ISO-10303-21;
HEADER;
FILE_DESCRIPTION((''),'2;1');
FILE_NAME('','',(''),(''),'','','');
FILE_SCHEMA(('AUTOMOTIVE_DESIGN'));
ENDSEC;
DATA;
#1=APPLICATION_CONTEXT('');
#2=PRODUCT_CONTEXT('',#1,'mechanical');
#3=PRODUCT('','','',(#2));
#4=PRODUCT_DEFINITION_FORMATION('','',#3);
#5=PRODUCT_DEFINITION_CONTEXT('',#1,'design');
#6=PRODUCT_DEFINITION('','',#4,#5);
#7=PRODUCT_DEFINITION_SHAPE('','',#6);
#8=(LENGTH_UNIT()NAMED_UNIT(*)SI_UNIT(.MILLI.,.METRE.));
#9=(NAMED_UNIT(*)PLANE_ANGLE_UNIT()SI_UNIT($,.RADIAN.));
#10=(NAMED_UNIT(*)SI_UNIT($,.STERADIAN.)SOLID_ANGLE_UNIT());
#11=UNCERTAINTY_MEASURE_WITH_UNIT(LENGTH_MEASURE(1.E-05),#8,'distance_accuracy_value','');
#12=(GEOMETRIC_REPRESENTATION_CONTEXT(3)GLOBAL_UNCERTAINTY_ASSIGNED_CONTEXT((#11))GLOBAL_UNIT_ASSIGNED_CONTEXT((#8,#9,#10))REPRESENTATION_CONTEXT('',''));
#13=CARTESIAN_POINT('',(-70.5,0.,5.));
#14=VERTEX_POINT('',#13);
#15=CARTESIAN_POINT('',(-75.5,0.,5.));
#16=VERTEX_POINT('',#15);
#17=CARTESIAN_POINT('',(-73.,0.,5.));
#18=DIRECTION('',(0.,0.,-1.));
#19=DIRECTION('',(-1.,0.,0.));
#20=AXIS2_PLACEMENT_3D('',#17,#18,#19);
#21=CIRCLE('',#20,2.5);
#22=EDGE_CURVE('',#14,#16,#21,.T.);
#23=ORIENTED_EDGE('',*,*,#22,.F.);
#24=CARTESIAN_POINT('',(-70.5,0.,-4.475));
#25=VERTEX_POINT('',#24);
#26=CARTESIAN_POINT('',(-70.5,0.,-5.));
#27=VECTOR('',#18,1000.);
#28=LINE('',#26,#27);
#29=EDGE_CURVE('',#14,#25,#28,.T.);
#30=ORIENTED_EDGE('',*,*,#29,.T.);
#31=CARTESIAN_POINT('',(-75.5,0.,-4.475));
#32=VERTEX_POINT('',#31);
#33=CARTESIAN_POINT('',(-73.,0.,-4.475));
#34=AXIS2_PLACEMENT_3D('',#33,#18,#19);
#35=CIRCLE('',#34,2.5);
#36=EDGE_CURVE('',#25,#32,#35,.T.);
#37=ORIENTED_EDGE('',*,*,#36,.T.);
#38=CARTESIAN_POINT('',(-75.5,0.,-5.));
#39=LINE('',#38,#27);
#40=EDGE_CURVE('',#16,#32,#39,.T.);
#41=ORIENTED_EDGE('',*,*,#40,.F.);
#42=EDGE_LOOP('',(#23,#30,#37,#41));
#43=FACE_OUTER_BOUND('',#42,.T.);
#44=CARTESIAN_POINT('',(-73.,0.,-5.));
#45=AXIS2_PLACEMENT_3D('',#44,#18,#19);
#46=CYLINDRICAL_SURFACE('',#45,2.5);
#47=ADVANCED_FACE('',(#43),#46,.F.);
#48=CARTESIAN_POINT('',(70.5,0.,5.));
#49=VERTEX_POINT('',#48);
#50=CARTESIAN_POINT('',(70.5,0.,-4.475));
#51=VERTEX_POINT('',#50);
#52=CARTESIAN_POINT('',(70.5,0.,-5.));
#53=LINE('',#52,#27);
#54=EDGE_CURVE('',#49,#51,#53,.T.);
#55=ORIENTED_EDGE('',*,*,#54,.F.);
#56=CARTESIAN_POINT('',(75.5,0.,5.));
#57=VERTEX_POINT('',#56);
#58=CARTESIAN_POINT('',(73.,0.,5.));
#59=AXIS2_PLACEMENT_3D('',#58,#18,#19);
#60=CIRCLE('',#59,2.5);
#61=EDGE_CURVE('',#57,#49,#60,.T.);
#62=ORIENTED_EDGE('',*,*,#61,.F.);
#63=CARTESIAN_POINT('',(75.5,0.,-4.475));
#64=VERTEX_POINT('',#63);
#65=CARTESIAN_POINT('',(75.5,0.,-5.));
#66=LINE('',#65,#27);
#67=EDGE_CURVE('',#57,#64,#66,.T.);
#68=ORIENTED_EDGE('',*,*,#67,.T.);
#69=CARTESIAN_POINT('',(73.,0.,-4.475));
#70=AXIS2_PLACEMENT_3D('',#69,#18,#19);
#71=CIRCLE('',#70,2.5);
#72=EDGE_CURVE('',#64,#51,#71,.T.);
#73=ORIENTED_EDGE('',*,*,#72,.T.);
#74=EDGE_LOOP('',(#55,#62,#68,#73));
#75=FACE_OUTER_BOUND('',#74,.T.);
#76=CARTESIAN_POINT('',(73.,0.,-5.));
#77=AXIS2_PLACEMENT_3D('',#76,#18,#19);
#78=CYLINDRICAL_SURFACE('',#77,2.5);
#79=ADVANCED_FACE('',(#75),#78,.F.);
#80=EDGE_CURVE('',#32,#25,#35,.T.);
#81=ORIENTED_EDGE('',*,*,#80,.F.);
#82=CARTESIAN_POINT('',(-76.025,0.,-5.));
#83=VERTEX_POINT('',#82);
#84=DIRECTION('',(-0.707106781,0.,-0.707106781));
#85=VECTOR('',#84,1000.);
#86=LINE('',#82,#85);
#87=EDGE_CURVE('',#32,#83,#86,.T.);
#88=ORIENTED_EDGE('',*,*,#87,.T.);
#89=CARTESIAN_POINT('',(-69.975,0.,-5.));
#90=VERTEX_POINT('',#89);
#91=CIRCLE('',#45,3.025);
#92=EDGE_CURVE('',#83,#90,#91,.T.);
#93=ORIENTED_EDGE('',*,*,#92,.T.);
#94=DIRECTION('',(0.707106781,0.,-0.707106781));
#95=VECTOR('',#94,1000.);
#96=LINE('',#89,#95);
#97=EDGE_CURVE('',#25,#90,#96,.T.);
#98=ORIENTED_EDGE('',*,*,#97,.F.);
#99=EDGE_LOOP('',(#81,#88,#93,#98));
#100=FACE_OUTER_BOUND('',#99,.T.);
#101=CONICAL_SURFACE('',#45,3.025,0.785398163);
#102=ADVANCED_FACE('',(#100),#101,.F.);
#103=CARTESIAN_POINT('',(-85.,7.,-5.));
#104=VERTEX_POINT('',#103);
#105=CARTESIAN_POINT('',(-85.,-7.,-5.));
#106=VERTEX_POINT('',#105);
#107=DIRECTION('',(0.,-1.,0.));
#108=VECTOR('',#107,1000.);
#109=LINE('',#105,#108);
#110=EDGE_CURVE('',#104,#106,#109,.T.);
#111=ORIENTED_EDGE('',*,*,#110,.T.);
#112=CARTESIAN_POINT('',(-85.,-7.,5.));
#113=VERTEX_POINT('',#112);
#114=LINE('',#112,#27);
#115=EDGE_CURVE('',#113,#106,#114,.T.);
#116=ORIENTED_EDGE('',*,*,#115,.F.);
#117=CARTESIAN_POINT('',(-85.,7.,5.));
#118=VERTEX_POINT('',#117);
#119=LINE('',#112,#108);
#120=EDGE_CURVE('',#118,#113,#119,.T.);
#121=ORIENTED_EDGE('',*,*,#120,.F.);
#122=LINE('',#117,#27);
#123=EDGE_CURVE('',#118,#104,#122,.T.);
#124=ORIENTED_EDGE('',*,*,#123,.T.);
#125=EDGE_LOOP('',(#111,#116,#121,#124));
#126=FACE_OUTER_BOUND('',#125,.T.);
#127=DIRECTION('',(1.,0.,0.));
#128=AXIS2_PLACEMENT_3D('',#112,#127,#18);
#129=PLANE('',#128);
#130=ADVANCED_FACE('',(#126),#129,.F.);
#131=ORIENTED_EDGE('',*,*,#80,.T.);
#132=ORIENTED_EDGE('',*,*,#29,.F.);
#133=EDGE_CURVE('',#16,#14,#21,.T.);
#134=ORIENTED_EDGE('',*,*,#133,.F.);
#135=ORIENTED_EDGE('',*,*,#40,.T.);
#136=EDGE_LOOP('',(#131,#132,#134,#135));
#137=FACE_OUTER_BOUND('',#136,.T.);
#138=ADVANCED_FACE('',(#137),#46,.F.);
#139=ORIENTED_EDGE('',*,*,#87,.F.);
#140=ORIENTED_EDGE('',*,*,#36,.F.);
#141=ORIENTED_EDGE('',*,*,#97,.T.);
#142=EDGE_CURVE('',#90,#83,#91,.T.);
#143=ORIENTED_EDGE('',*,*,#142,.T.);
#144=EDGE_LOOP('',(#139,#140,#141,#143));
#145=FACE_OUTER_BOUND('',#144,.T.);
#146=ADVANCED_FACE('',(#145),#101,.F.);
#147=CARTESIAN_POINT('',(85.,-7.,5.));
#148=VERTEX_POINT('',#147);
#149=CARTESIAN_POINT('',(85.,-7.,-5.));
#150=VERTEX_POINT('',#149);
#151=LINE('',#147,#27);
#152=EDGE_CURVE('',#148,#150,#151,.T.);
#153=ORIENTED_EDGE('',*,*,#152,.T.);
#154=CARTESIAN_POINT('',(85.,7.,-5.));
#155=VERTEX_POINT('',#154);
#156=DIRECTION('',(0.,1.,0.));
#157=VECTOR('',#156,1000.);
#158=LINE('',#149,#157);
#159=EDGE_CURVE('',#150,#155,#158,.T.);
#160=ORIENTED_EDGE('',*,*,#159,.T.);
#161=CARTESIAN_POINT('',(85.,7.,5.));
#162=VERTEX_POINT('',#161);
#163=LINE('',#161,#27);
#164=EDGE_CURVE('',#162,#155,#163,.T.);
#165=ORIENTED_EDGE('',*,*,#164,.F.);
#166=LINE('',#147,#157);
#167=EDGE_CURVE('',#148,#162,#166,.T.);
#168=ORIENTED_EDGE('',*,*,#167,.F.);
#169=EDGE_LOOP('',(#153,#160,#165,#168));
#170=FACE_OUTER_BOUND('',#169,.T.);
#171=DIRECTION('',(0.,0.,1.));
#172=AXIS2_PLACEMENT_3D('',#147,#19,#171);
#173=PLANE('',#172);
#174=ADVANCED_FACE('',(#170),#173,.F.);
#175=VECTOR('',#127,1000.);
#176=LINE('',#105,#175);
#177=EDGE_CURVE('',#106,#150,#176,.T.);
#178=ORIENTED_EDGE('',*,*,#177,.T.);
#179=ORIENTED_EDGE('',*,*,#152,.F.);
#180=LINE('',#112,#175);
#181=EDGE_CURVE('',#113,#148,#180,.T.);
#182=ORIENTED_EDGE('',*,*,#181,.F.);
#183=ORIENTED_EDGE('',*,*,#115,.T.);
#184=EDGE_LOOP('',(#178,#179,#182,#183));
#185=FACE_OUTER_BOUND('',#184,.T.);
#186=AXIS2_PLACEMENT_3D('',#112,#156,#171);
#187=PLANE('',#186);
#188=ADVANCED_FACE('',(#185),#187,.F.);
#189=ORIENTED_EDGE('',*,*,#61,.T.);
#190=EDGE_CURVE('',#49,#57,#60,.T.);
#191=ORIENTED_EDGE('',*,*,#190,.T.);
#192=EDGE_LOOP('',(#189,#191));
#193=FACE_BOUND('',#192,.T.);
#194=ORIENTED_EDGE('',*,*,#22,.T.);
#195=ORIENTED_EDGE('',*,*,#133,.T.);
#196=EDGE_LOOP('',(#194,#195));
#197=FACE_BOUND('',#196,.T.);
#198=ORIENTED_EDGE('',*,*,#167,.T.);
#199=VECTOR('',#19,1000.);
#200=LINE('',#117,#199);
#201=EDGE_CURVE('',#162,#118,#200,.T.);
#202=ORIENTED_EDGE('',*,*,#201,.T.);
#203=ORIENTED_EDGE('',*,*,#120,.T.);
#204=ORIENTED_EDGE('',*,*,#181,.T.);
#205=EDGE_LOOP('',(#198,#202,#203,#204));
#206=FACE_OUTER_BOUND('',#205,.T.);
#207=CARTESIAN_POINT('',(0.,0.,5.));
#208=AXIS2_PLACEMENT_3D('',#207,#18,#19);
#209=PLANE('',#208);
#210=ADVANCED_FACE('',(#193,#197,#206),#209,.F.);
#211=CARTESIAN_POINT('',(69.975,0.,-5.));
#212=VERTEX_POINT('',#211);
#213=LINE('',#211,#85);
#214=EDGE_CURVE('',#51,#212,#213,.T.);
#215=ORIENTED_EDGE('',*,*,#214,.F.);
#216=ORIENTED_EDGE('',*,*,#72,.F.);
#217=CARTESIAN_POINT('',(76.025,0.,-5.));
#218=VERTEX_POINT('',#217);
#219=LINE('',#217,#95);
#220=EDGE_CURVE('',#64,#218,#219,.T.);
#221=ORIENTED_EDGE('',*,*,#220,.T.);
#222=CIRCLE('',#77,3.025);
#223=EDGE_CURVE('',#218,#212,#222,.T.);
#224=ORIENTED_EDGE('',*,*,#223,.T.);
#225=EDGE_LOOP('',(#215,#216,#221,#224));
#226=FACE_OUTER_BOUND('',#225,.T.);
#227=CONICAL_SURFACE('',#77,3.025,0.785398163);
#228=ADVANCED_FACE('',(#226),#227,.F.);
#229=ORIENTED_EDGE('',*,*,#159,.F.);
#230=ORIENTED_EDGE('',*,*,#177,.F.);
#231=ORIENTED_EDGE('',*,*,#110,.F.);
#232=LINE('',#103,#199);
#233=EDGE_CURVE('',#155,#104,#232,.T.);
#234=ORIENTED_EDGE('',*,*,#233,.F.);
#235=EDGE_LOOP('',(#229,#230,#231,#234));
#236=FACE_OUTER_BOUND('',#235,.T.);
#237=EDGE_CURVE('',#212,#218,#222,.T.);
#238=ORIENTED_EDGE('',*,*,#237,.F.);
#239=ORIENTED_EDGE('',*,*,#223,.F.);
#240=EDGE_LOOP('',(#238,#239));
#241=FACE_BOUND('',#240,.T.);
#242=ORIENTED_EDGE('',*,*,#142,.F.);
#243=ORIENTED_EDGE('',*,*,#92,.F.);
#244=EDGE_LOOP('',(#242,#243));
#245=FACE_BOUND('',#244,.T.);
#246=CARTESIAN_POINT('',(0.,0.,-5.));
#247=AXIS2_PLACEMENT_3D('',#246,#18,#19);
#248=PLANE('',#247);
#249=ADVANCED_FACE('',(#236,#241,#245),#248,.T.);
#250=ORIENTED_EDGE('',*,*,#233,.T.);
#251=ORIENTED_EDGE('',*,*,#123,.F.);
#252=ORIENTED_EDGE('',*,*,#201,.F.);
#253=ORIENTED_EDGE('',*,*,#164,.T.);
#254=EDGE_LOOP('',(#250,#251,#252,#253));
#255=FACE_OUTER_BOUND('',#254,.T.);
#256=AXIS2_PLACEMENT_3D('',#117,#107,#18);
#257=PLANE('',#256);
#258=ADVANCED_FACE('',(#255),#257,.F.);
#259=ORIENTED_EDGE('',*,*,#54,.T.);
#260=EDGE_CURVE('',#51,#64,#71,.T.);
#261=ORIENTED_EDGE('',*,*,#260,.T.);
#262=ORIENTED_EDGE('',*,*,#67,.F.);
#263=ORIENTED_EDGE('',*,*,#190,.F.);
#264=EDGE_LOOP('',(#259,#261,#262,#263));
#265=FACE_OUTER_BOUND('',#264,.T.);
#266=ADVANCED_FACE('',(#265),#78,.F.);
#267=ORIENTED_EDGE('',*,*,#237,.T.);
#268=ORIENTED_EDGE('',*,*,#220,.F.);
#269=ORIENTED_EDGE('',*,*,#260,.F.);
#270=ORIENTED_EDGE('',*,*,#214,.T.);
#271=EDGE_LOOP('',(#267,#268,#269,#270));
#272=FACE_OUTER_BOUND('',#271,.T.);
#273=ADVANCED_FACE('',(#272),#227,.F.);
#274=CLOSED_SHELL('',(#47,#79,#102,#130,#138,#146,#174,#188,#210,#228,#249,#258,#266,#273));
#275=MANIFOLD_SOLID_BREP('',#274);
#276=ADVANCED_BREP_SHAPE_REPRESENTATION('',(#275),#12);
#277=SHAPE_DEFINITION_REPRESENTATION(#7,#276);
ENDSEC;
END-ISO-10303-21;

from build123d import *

# Parameters (mm, degrees)
SKETCH_1_W                   = 170
SKETCH_1_H                   = 14
EXTRUDE_1_DEPTH              = 5
HOLE_WIZARD_M6_1_D           = 5
HOLE_WIZARD_M6_1_CSINK_D     = 6.05
HOLE_WIZARD_M6_1_CSINK_ANGLE = 90


with BuildPart() as part:
    # 草图1 → 凸台-拉伸1 (new, symmetric)
    with BuildSketch(Plane.XY):
        Rectangle(SKETCH_1_W, SKETCH_1_H)
    extrude(amount=EXTRUDE_1_DEPTH, both=True)

    # M6 螺纹孔1 (through all)
    with Locations(Plane(origin=(-73, 0, -5), x_dir=(-1, 0, 0), z_dir=(0, 0, -1))):
        with Locations((0, 0)):
            hole_wizard_m6_1 = CounterSinkHole(HOLE_WIZARD_M6_1_D / 2, HOLE_WIZARD_M6_1_CSINK_D / 2, counter_sink_angle=HOLE_WIZARD_M6_1_CSINK_ANGLE)

    # 镜向1: M6 螺纹孔1 across plane
    add(hole_wizard_m6_1.mirror(Plane(origin=(0, 0, 0), x_dir=(0, 0, 1), z_dir=(1, 0, 0))), mode=Mode.SUBTRACT)


solid = part.part
